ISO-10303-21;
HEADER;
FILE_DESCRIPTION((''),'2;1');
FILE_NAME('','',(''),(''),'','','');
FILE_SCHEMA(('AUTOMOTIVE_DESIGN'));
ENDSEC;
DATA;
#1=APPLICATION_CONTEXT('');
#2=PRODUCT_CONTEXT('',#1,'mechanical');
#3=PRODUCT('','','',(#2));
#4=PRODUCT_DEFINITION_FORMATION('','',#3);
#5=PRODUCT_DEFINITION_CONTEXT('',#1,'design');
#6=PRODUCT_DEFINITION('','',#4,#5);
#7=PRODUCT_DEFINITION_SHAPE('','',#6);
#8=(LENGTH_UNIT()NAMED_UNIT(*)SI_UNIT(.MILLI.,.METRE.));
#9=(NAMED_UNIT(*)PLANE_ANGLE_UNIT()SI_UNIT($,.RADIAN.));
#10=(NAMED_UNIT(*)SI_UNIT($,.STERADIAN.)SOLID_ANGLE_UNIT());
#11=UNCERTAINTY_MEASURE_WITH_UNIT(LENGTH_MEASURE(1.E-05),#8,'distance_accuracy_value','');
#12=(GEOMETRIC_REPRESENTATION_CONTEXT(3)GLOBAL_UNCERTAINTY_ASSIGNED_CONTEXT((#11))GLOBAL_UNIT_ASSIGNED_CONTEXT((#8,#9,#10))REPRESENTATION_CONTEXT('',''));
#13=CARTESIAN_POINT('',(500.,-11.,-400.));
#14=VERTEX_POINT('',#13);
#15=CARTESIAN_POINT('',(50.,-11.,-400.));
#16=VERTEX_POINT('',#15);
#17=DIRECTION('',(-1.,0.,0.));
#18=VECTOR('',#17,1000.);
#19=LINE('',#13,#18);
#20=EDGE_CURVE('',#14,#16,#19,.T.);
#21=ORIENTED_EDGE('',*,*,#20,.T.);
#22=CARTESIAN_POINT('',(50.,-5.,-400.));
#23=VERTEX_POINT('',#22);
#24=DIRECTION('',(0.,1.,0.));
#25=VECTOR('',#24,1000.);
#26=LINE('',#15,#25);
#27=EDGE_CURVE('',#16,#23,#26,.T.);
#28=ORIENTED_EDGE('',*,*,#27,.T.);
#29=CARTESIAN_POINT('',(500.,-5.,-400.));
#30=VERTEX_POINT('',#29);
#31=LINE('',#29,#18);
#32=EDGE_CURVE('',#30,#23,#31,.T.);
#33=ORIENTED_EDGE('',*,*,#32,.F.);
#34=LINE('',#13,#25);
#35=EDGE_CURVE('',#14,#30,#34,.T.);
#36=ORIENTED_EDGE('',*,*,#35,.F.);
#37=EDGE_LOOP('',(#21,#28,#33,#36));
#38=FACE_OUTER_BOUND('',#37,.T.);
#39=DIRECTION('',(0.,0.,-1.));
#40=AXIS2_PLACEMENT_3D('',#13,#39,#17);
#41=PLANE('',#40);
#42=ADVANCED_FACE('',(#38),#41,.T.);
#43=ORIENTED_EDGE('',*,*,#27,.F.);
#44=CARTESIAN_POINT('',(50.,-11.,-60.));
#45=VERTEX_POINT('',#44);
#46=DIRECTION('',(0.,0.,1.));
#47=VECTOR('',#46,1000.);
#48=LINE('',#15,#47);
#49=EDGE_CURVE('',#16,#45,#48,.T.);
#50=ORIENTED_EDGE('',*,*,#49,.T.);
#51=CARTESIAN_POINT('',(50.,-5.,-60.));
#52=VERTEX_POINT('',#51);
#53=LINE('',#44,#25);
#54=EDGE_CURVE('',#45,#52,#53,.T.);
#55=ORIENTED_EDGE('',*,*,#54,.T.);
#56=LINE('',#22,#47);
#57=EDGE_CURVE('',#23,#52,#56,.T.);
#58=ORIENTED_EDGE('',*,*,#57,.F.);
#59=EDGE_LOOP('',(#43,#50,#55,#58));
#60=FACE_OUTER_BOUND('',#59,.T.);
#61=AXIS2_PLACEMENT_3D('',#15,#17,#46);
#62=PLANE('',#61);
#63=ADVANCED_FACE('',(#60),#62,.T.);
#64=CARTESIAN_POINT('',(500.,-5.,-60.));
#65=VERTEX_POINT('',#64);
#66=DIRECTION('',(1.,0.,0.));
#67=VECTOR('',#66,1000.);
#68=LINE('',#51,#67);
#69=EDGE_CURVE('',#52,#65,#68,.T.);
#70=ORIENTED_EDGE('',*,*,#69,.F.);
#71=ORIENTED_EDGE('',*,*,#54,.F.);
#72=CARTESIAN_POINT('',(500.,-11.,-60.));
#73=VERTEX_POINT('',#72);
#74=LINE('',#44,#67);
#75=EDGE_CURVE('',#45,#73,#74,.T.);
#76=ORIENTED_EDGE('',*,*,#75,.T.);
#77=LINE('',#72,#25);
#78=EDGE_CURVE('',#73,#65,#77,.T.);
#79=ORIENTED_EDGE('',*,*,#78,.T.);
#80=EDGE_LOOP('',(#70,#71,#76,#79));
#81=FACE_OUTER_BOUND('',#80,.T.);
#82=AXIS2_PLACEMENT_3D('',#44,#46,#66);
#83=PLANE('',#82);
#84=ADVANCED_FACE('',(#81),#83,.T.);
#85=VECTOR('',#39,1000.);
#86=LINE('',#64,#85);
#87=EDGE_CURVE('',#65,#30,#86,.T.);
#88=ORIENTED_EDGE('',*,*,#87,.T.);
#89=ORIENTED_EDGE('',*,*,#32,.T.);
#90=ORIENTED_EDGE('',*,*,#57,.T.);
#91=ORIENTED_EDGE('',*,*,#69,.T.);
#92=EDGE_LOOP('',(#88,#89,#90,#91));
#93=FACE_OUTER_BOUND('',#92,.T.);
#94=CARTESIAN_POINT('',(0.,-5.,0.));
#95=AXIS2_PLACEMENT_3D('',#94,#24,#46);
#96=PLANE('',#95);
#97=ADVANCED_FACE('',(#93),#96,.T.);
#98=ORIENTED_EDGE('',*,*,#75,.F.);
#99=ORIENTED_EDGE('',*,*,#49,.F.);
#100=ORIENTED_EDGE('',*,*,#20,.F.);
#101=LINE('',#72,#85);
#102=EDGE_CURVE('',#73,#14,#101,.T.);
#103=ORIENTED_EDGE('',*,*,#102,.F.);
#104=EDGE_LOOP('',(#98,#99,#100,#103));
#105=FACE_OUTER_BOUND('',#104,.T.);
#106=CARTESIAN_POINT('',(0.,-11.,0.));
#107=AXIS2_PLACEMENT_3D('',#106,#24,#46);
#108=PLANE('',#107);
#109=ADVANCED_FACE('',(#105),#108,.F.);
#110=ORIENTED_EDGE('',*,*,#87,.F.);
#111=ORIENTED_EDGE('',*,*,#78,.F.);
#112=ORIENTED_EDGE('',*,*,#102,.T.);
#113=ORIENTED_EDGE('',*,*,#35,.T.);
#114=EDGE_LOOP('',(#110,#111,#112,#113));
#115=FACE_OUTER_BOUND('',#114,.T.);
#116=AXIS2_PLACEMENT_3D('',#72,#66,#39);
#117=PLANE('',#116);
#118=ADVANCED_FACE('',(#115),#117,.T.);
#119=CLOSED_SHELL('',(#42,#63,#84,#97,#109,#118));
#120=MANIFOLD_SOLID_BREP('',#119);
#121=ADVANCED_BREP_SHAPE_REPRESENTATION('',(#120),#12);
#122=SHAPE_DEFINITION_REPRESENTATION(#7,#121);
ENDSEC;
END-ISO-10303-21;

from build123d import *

# Parameters (mm, degrees)
SKETCH1_W           = 450
SKETCH1_H           = 340
BOSS_EXTRUDE1_DEPTH = 6


with BuildPart() as part:
    # Sketch1 → Boss-Extrude1 (new body)
    with BuildSketch(Plane(origin=(0, -5, 0), x_dir=(1, 0, 0), z_dir=(0, 1, 0))):
        with Locations((275, 230)):
            Rectangle(SKETCH1_W, SKETCH1_H)
    extrude(amount=-BOSS_EXTRUDE1_DEPTH)


solid = part.part
